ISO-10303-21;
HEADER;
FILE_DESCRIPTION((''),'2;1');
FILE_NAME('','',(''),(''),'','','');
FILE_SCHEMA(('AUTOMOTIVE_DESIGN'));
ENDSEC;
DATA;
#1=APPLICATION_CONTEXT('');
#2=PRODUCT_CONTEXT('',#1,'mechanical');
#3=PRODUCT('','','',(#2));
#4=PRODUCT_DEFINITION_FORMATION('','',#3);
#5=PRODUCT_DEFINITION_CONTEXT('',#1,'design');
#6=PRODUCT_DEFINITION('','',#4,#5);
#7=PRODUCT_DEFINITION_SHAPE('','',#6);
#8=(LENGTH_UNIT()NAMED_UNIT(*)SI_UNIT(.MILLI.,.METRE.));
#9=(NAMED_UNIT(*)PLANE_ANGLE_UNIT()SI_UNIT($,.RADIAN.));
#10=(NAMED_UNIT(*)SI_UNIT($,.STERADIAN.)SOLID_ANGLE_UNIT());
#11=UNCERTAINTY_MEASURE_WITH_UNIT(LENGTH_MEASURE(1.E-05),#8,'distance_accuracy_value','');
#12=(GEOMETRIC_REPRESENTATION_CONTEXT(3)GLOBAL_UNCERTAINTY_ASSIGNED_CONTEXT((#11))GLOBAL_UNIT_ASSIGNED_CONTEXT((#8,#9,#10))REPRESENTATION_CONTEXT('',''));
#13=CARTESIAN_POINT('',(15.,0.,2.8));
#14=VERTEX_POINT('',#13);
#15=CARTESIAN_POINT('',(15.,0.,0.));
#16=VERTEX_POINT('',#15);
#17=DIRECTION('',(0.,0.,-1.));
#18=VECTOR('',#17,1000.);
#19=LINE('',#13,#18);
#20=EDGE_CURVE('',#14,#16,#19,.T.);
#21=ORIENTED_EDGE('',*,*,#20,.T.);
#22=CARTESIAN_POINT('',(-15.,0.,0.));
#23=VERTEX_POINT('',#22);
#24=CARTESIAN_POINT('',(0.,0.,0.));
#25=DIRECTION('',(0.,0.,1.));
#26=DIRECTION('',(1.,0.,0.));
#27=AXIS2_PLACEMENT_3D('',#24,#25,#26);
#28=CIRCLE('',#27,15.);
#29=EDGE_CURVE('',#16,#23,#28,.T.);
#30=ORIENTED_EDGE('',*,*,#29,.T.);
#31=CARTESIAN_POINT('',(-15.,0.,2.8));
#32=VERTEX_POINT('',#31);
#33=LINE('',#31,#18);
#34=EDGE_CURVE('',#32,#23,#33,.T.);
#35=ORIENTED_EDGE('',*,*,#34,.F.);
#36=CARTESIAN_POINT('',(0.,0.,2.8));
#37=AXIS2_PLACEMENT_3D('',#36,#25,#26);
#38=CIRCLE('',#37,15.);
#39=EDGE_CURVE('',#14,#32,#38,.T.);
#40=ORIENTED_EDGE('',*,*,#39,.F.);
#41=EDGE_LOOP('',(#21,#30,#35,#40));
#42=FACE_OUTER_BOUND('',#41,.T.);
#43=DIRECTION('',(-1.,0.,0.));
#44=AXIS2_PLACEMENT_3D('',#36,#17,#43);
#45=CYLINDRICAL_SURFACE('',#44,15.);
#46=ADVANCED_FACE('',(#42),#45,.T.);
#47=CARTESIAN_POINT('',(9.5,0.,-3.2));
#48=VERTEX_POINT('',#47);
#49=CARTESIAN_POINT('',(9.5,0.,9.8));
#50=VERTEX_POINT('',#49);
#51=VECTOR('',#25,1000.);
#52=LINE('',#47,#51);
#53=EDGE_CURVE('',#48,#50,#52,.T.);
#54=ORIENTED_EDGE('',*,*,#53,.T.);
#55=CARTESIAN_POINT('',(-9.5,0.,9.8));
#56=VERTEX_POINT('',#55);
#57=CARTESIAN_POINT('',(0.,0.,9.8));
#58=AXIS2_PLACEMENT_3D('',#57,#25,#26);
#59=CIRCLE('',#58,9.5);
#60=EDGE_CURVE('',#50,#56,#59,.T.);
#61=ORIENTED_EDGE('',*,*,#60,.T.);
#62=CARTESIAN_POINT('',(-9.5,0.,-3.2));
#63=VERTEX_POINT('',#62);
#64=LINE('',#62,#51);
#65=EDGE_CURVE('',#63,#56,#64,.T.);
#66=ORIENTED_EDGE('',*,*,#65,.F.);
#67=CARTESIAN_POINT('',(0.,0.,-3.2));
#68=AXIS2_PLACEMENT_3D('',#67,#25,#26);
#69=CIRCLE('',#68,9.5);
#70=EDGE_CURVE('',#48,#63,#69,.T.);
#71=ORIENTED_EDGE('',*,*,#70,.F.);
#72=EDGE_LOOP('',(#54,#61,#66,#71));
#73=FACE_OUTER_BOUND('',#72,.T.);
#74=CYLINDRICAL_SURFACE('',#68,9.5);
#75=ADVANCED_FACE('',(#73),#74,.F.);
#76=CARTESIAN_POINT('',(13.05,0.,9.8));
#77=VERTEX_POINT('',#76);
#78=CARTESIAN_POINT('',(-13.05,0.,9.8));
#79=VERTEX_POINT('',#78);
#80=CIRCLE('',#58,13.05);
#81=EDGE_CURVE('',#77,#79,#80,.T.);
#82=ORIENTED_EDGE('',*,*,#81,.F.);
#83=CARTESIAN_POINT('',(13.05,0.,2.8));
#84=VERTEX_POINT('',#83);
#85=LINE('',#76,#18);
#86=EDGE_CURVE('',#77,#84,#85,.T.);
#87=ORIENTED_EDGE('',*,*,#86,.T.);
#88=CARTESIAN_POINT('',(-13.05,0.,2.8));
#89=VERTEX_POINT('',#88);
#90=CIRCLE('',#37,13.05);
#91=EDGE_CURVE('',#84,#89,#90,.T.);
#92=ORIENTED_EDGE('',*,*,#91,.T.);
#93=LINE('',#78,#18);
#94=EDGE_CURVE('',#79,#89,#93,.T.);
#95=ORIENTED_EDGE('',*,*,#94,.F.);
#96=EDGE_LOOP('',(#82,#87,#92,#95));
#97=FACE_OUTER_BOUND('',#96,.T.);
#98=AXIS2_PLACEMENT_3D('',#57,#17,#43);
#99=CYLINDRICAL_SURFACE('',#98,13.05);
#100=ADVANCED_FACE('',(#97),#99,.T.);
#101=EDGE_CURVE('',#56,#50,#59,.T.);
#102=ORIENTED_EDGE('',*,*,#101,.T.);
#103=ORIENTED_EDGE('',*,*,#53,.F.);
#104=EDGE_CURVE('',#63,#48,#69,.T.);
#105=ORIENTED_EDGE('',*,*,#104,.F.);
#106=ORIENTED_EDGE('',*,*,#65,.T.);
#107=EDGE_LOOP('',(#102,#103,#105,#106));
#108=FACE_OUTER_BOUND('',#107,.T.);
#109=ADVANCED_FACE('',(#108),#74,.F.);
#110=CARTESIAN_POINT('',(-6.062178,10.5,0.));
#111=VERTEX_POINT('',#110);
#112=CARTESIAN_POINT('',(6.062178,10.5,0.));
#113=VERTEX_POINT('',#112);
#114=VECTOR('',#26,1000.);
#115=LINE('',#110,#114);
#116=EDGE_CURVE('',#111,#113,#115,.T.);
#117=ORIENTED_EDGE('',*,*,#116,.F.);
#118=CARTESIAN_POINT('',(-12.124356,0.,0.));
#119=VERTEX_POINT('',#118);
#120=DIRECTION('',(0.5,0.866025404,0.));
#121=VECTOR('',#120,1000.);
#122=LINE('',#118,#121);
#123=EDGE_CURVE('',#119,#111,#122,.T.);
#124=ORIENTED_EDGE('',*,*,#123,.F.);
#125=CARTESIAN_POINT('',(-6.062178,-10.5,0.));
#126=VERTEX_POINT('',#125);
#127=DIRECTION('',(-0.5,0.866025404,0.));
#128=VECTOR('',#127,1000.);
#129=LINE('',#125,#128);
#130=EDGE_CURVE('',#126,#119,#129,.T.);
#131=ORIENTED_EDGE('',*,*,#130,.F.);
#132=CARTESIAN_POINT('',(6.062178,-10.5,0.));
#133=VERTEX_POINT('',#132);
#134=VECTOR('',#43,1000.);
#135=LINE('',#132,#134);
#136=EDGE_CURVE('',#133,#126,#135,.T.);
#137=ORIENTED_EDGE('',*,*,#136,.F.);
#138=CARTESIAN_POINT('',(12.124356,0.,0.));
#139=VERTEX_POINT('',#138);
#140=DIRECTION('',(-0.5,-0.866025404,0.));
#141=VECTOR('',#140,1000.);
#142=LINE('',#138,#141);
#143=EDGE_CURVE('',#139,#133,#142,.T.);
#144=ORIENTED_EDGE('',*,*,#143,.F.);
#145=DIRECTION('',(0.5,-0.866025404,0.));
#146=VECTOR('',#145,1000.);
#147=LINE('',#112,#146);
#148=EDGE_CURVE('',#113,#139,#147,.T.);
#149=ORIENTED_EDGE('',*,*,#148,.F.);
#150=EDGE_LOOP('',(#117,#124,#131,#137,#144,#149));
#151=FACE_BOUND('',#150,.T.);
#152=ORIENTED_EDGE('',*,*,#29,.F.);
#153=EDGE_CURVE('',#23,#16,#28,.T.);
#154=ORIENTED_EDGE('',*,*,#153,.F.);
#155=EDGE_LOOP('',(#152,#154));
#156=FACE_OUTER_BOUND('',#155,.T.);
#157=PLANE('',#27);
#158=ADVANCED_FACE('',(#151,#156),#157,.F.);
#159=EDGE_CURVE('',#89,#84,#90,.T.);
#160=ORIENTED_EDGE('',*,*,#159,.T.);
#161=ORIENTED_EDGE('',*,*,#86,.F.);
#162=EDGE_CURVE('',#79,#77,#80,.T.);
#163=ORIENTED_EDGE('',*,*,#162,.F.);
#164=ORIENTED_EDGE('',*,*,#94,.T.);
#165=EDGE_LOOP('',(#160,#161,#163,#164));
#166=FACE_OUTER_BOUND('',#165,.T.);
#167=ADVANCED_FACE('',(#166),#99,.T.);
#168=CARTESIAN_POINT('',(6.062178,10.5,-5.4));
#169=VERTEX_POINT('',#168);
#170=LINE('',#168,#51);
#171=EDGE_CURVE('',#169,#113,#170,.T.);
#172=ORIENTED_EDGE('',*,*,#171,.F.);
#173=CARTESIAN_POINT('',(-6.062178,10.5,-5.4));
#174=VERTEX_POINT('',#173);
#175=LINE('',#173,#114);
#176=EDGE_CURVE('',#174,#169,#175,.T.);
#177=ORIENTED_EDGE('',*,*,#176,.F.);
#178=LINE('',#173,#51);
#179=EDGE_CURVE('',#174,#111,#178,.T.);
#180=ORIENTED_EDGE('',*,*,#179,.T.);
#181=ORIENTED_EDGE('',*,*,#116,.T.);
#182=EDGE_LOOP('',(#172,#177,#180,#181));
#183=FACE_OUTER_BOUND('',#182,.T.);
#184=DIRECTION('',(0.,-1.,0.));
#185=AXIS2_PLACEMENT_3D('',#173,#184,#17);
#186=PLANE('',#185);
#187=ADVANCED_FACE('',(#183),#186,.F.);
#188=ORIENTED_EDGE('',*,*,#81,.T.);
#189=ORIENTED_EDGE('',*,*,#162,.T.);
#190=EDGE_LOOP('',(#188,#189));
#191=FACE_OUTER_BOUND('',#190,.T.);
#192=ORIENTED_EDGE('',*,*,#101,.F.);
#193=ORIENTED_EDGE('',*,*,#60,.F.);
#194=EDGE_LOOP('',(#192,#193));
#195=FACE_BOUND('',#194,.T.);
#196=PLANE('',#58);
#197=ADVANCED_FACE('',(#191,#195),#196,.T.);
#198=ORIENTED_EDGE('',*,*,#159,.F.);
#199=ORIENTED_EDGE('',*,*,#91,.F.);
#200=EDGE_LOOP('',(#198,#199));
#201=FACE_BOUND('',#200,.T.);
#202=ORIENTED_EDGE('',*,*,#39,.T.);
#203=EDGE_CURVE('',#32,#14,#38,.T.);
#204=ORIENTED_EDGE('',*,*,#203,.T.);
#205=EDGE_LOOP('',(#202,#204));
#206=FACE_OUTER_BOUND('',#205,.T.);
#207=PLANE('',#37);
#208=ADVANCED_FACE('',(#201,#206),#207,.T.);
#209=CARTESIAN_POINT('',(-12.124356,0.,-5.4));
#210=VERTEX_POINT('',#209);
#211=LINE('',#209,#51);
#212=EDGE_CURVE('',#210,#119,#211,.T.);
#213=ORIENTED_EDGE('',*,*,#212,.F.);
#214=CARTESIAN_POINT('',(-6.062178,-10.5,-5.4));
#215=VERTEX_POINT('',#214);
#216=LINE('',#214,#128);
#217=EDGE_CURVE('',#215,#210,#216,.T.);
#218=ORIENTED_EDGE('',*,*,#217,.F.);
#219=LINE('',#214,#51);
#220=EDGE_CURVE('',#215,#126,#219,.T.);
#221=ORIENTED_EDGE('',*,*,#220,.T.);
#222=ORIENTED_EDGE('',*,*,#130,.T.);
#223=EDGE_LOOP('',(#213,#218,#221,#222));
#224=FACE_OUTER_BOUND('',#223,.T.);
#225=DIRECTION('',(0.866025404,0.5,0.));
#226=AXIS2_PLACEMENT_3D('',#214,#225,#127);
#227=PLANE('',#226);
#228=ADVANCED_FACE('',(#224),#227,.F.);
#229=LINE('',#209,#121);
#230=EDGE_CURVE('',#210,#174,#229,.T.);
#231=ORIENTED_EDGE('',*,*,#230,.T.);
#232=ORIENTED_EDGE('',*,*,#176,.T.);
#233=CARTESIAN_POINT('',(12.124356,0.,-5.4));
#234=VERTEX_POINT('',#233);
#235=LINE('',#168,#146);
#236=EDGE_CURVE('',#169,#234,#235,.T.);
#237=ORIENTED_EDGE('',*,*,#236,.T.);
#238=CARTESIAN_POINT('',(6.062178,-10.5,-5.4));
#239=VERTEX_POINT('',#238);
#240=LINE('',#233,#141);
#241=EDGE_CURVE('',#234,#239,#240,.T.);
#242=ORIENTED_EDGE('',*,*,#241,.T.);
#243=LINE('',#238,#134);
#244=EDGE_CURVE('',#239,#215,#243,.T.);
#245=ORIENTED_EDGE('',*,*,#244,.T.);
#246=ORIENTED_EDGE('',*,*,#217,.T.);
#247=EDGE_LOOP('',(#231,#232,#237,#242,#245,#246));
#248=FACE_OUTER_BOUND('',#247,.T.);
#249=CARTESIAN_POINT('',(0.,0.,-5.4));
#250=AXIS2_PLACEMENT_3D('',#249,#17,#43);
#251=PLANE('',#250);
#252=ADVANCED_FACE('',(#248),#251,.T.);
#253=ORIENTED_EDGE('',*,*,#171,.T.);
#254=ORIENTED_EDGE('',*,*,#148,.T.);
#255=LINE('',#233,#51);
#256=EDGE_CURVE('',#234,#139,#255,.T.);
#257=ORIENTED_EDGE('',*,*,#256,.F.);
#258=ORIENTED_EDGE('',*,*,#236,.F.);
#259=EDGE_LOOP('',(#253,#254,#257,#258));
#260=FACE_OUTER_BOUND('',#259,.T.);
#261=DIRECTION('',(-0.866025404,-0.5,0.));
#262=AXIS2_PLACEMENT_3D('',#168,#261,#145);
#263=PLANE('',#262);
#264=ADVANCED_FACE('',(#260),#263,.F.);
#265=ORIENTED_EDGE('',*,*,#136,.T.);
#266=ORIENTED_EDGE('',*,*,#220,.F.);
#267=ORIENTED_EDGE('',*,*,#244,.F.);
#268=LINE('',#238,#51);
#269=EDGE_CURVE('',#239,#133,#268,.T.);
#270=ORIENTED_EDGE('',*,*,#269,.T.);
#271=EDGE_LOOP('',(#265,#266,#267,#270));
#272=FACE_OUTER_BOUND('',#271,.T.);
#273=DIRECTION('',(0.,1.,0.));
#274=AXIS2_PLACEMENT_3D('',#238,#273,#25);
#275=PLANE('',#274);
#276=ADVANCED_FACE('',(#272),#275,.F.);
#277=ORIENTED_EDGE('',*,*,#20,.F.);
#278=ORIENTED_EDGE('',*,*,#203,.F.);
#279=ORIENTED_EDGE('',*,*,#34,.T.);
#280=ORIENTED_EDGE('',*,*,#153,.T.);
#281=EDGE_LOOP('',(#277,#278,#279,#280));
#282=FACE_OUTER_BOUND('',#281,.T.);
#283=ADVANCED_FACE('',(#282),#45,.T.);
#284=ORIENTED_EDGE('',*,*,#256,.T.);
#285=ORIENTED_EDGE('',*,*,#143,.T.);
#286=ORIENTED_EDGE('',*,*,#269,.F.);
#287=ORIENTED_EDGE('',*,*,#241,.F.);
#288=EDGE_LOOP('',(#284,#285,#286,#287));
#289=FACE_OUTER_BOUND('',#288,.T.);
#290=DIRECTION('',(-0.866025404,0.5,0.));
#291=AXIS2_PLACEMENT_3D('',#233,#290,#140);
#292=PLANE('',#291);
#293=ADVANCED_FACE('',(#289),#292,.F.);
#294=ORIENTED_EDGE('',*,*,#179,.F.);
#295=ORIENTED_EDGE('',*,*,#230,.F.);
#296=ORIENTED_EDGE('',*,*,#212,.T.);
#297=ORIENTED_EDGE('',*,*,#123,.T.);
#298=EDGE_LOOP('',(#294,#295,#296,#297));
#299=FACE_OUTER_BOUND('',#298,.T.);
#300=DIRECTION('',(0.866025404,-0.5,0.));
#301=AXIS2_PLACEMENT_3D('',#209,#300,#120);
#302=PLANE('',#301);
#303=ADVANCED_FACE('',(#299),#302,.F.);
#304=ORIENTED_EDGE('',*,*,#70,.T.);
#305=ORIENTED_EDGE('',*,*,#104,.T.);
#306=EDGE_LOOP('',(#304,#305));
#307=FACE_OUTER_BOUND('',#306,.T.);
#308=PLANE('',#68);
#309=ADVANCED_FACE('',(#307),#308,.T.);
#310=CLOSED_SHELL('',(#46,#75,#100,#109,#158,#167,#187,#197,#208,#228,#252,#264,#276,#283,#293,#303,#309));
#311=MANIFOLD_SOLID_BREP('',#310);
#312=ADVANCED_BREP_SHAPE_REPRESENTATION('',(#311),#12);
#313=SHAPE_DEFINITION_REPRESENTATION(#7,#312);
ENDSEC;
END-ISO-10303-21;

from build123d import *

# Parameters (mm, degrees)
SKETCH_1_R          = 15
EXTRUDE_1_DEPTH     = 2.8
EXTRUDE_2_DEPTH     = 5.4
SKETCH_3_R          = 13.05
EXTRUDE_3_DEPTH     = 7
SKETCH_4_R          = 9.5
CUT_EXTRUDE_1_DEPTH = 13


with BuildPart() as part:
    # 草图1 → 凸台-拉伸1 (new body)
    with BuildSketch(Plane.XY):
        Circle(SKETCH_1_R)
    extrude(amount=EXTRUDE_1_DEPTH)

    # 草图2 → 凸台-拉伸2 (add)
    with BuildSketch(Plane(origin=(0, 0, 0), x_dir=(-1, 0, 0), z_dir=(0, 0, -1))):
        Polygon((6.062177826, -10.5), (12.124355653, 0), (6.062177826, 10.5), (-6.062177826, 10.5), (-12.124355653, 0), (-6.062177826, -10.5), align=None)
    extrude(amount=EXTRUDE_2_DEPTH)

    # 草图3 → 凸台-拉伸3 (add)
    with BuildSketch(Plane.XY.offset(2.8)):
        Circle(SKETCH_3_R)
    extrude(amount=EXTRUDE_3_DEPTH)

    # 草图4 → 切除-拉伸1 (cut)
    with BuildSketch(Plane.XY.offset(9.8)):
        Circle(SKETCH_4_R)
    extrude(amount=-CUT_EXTRUDE_1_DEPTH, mode=Mode.SUBTRACT)


solid = part.part
